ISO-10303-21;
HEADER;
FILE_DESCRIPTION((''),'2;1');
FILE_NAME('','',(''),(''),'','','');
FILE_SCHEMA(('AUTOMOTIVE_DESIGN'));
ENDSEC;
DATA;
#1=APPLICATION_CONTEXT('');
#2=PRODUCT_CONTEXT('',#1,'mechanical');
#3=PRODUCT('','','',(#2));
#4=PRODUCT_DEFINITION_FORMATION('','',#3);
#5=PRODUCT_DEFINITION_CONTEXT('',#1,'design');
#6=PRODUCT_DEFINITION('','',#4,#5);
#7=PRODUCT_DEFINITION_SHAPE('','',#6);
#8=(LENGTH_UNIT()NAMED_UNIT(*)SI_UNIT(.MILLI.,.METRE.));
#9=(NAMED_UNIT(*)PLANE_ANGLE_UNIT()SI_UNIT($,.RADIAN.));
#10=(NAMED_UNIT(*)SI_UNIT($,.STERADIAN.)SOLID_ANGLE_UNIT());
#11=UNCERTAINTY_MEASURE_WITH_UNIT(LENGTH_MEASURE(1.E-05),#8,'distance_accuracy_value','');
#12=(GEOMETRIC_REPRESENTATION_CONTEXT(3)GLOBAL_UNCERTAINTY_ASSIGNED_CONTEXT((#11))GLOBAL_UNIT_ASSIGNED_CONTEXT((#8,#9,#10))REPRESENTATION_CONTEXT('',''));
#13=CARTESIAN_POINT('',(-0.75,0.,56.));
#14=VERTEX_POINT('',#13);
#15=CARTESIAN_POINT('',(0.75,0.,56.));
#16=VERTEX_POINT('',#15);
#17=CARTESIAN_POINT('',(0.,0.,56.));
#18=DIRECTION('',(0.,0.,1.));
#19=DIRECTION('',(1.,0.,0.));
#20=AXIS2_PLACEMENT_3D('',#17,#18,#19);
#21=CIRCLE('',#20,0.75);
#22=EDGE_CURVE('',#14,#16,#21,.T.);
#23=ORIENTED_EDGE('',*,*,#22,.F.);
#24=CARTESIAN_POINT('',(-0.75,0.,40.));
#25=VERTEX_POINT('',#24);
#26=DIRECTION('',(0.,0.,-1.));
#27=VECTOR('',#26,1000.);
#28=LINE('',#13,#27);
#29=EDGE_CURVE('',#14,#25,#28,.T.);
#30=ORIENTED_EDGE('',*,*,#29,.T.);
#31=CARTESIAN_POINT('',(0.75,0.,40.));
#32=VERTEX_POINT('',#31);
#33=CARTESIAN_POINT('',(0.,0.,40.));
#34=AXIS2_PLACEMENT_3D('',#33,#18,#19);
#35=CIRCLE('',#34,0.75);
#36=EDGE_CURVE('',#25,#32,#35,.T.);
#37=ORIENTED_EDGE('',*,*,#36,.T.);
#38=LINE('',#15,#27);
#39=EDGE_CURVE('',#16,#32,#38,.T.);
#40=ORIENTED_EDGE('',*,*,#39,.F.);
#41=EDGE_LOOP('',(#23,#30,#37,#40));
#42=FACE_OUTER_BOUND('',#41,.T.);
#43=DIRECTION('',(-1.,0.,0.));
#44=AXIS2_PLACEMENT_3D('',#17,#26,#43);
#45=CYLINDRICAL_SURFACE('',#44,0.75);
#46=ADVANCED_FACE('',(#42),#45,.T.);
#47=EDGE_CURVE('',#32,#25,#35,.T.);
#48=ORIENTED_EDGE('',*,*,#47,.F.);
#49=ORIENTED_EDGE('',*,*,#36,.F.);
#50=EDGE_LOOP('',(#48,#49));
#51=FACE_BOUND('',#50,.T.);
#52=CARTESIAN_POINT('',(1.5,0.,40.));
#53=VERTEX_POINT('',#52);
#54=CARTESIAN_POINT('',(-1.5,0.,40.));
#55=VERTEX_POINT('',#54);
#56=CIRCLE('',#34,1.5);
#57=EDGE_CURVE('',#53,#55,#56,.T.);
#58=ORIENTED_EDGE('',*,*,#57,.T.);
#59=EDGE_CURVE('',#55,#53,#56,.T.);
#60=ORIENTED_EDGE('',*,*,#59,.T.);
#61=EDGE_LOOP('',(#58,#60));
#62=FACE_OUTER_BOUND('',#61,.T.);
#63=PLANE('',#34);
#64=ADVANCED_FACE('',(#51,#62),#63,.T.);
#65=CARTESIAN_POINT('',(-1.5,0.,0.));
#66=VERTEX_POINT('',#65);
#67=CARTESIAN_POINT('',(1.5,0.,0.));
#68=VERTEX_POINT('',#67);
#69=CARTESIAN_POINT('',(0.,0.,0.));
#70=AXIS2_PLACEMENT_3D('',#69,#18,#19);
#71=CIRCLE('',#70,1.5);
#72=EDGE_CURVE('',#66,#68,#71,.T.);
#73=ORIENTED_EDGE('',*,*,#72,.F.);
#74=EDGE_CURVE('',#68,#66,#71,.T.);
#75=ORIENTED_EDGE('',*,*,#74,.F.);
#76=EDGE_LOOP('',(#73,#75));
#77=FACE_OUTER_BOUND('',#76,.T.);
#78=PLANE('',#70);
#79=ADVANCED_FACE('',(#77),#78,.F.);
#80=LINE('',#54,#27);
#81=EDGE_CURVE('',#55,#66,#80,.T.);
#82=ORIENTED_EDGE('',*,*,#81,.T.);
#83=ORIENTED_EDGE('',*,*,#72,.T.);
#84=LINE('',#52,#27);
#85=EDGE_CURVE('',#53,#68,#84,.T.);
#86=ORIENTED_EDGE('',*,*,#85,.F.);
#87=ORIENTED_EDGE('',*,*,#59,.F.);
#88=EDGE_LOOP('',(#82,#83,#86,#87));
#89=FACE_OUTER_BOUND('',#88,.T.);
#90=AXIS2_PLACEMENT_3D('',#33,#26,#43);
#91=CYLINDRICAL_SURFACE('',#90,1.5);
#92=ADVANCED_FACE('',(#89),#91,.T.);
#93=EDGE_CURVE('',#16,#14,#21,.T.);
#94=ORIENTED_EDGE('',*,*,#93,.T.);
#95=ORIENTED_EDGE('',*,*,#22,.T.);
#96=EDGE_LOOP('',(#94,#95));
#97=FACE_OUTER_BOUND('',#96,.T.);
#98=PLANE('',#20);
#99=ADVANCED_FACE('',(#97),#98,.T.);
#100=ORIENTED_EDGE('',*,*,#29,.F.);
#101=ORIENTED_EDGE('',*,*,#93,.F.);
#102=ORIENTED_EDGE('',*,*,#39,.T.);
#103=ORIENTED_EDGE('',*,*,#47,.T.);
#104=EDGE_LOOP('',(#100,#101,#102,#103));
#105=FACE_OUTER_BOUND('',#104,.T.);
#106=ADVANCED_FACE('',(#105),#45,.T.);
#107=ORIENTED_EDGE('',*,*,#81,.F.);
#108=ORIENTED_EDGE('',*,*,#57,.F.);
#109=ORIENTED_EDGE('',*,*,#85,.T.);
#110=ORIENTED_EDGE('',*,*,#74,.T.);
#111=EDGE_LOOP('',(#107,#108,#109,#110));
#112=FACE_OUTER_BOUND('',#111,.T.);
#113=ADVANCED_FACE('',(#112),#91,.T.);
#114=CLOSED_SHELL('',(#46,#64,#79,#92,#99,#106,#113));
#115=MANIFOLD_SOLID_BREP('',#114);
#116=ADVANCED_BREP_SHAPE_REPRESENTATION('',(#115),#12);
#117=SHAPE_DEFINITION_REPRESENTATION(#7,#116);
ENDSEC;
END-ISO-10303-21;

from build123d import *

# Parameters (mm, degrees)
SKETCH1_R           = 1.5
BOSS_EXTRUDE1_DEPTH = 40
SKETCH2_R           = 0.75
BOSS_EXTRUDE2_DEPTH = 16


with BuildPart() as part:
    # Sketch1 → Boss-Extrude1 (new body)
    with BuildSketch(Plane.XY):
        Circle(SKETCH1_R)
    extrude(amount=BOSS_EXTRUDE1_DEPTH)

    # Sketch2 → Boss-Extrude2 (add)
    with BuildSketch(Plane.XY.offset(40)):
        Circle(SKETCH2_R)
    extrude(amount=BOSS_EXTRUDE2_DEPTH)


solid = part.part
